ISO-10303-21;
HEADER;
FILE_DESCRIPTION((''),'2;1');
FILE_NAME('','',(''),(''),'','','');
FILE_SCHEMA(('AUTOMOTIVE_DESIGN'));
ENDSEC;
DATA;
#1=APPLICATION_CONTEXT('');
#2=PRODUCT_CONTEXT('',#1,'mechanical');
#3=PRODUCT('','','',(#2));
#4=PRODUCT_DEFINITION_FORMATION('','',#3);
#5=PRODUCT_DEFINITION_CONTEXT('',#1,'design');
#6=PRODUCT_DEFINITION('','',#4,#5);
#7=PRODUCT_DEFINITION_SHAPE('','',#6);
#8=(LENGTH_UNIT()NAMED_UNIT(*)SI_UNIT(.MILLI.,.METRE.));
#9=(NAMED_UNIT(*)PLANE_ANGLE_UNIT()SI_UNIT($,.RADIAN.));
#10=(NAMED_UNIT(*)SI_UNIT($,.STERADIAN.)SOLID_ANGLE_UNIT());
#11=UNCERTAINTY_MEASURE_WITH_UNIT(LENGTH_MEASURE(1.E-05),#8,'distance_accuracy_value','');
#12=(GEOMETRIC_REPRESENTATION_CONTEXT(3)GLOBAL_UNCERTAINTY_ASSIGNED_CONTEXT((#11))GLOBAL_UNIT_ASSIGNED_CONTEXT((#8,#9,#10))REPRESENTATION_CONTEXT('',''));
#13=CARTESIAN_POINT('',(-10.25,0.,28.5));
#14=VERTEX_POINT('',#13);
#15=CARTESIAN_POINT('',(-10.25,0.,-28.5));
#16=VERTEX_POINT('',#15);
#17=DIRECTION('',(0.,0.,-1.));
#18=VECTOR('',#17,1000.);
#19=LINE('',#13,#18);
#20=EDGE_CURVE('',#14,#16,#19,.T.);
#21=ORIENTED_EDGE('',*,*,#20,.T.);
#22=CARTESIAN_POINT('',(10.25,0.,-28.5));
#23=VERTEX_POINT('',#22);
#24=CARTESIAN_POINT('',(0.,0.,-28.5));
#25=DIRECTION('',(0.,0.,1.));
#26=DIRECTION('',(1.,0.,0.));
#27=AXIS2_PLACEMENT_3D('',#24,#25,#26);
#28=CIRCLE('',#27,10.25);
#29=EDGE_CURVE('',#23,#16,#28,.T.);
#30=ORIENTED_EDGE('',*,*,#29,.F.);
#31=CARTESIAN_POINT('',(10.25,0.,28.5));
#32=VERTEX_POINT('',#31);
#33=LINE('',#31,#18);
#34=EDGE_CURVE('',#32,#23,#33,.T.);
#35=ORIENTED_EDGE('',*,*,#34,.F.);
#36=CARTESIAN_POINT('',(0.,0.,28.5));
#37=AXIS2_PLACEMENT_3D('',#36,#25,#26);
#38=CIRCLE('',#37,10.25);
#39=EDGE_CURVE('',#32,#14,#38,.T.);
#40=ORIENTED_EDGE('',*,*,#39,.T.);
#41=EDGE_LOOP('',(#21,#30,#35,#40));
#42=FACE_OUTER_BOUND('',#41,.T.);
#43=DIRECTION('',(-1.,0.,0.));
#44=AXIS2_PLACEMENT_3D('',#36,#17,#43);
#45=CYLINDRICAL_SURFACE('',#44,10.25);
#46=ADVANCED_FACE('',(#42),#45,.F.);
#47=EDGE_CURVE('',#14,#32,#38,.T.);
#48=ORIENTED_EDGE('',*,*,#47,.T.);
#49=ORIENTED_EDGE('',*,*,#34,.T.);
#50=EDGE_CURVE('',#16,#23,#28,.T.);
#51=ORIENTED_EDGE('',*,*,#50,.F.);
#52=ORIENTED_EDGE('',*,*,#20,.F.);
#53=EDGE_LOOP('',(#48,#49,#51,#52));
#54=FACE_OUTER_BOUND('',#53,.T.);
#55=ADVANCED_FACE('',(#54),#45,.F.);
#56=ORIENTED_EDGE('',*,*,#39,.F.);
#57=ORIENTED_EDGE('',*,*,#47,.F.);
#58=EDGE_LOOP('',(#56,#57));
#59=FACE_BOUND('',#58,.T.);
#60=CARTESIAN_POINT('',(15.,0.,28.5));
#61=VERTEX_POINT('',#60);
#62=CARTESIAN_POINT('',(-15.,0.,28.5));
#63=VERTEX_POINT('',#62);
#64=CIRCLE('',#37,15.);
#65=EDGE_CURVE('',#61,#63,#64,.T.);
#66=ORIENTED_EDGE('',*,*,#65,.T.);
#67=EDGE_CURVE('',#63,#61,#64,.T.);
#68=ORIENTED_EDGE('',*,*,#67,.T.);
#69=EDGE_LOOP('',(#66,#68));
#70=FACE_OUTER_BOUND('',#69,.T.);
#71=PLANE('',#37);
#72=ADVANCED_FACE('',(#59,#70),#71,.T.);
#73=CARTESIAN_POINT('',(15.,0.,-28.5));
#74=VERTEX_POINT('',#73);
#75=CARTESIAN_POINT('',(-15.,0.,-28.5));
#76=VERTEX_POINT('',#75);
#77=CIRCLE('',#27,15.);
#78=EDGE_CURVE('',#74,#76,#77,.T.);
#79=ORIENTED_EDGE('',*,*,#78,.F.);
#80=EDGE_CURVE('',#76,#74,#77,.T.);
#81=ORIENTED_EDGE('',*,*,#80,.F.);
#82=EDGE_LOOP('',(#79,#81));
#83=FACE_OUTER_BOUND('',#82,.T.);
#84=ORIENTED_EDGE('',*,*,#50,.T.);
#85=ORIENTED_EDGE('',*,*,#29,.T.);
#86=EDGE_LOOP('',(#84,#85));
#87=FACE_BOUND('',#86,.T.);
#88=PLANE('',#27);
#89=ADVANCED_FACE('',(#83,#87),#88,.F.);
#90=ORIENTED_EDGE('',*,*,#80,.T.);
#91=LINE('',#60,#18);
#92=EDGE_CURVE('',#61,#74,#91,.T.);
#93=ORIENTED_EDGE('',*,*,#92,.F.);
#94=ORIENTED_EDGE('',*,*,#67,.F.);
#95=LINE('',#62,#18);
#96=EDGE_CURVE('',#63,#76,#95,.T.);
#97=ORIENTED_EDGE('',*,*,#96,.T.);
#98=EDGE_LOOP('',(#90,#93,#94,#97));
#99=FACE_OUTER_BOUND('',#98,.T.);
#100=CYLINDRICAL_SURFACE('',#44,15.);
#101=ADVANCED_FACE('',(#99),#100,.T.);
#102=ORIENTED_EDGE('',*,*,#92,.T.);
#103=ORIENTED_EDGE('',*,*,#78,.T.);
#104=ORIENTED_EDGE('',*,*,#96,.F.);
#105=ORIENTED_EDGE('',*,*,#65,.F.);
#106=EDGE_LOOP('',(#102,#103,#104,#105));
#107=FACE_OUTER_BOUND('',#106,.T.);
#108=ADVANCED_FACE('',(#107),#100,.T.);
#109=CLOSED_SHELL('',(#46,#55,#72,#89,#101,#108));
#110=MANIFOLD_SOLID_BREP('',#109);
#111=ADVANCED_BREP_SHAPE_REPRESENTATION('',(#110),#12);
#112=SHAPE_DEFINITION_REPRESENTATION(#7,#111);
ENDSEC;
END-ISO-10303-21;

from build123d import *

# Parameters (mm, degrees)
SKETCH_1_R      = 15
SKETCH_1_R_2    = 10.25
EXTRUDE_1_DEPTH = 28.5


with BuildPart() as part:
    # 草图1 → 凸台-拉伸1 (new, symmetric)
    with BuildSketch(Plane.XY):
        with Locations(Location((0, 0, 0), (0, 0, 180))):
            Circle(SKETCH_1_R)
        with Locations(Location((0, 0, 0), (0, 0, 180))):
            Circle(SKETCH_1_R_2, mode=Mode.SUBTRACT)
    extrude(amount=EXTRUDE_1_DEPTH, both=True)


solid = part.part
